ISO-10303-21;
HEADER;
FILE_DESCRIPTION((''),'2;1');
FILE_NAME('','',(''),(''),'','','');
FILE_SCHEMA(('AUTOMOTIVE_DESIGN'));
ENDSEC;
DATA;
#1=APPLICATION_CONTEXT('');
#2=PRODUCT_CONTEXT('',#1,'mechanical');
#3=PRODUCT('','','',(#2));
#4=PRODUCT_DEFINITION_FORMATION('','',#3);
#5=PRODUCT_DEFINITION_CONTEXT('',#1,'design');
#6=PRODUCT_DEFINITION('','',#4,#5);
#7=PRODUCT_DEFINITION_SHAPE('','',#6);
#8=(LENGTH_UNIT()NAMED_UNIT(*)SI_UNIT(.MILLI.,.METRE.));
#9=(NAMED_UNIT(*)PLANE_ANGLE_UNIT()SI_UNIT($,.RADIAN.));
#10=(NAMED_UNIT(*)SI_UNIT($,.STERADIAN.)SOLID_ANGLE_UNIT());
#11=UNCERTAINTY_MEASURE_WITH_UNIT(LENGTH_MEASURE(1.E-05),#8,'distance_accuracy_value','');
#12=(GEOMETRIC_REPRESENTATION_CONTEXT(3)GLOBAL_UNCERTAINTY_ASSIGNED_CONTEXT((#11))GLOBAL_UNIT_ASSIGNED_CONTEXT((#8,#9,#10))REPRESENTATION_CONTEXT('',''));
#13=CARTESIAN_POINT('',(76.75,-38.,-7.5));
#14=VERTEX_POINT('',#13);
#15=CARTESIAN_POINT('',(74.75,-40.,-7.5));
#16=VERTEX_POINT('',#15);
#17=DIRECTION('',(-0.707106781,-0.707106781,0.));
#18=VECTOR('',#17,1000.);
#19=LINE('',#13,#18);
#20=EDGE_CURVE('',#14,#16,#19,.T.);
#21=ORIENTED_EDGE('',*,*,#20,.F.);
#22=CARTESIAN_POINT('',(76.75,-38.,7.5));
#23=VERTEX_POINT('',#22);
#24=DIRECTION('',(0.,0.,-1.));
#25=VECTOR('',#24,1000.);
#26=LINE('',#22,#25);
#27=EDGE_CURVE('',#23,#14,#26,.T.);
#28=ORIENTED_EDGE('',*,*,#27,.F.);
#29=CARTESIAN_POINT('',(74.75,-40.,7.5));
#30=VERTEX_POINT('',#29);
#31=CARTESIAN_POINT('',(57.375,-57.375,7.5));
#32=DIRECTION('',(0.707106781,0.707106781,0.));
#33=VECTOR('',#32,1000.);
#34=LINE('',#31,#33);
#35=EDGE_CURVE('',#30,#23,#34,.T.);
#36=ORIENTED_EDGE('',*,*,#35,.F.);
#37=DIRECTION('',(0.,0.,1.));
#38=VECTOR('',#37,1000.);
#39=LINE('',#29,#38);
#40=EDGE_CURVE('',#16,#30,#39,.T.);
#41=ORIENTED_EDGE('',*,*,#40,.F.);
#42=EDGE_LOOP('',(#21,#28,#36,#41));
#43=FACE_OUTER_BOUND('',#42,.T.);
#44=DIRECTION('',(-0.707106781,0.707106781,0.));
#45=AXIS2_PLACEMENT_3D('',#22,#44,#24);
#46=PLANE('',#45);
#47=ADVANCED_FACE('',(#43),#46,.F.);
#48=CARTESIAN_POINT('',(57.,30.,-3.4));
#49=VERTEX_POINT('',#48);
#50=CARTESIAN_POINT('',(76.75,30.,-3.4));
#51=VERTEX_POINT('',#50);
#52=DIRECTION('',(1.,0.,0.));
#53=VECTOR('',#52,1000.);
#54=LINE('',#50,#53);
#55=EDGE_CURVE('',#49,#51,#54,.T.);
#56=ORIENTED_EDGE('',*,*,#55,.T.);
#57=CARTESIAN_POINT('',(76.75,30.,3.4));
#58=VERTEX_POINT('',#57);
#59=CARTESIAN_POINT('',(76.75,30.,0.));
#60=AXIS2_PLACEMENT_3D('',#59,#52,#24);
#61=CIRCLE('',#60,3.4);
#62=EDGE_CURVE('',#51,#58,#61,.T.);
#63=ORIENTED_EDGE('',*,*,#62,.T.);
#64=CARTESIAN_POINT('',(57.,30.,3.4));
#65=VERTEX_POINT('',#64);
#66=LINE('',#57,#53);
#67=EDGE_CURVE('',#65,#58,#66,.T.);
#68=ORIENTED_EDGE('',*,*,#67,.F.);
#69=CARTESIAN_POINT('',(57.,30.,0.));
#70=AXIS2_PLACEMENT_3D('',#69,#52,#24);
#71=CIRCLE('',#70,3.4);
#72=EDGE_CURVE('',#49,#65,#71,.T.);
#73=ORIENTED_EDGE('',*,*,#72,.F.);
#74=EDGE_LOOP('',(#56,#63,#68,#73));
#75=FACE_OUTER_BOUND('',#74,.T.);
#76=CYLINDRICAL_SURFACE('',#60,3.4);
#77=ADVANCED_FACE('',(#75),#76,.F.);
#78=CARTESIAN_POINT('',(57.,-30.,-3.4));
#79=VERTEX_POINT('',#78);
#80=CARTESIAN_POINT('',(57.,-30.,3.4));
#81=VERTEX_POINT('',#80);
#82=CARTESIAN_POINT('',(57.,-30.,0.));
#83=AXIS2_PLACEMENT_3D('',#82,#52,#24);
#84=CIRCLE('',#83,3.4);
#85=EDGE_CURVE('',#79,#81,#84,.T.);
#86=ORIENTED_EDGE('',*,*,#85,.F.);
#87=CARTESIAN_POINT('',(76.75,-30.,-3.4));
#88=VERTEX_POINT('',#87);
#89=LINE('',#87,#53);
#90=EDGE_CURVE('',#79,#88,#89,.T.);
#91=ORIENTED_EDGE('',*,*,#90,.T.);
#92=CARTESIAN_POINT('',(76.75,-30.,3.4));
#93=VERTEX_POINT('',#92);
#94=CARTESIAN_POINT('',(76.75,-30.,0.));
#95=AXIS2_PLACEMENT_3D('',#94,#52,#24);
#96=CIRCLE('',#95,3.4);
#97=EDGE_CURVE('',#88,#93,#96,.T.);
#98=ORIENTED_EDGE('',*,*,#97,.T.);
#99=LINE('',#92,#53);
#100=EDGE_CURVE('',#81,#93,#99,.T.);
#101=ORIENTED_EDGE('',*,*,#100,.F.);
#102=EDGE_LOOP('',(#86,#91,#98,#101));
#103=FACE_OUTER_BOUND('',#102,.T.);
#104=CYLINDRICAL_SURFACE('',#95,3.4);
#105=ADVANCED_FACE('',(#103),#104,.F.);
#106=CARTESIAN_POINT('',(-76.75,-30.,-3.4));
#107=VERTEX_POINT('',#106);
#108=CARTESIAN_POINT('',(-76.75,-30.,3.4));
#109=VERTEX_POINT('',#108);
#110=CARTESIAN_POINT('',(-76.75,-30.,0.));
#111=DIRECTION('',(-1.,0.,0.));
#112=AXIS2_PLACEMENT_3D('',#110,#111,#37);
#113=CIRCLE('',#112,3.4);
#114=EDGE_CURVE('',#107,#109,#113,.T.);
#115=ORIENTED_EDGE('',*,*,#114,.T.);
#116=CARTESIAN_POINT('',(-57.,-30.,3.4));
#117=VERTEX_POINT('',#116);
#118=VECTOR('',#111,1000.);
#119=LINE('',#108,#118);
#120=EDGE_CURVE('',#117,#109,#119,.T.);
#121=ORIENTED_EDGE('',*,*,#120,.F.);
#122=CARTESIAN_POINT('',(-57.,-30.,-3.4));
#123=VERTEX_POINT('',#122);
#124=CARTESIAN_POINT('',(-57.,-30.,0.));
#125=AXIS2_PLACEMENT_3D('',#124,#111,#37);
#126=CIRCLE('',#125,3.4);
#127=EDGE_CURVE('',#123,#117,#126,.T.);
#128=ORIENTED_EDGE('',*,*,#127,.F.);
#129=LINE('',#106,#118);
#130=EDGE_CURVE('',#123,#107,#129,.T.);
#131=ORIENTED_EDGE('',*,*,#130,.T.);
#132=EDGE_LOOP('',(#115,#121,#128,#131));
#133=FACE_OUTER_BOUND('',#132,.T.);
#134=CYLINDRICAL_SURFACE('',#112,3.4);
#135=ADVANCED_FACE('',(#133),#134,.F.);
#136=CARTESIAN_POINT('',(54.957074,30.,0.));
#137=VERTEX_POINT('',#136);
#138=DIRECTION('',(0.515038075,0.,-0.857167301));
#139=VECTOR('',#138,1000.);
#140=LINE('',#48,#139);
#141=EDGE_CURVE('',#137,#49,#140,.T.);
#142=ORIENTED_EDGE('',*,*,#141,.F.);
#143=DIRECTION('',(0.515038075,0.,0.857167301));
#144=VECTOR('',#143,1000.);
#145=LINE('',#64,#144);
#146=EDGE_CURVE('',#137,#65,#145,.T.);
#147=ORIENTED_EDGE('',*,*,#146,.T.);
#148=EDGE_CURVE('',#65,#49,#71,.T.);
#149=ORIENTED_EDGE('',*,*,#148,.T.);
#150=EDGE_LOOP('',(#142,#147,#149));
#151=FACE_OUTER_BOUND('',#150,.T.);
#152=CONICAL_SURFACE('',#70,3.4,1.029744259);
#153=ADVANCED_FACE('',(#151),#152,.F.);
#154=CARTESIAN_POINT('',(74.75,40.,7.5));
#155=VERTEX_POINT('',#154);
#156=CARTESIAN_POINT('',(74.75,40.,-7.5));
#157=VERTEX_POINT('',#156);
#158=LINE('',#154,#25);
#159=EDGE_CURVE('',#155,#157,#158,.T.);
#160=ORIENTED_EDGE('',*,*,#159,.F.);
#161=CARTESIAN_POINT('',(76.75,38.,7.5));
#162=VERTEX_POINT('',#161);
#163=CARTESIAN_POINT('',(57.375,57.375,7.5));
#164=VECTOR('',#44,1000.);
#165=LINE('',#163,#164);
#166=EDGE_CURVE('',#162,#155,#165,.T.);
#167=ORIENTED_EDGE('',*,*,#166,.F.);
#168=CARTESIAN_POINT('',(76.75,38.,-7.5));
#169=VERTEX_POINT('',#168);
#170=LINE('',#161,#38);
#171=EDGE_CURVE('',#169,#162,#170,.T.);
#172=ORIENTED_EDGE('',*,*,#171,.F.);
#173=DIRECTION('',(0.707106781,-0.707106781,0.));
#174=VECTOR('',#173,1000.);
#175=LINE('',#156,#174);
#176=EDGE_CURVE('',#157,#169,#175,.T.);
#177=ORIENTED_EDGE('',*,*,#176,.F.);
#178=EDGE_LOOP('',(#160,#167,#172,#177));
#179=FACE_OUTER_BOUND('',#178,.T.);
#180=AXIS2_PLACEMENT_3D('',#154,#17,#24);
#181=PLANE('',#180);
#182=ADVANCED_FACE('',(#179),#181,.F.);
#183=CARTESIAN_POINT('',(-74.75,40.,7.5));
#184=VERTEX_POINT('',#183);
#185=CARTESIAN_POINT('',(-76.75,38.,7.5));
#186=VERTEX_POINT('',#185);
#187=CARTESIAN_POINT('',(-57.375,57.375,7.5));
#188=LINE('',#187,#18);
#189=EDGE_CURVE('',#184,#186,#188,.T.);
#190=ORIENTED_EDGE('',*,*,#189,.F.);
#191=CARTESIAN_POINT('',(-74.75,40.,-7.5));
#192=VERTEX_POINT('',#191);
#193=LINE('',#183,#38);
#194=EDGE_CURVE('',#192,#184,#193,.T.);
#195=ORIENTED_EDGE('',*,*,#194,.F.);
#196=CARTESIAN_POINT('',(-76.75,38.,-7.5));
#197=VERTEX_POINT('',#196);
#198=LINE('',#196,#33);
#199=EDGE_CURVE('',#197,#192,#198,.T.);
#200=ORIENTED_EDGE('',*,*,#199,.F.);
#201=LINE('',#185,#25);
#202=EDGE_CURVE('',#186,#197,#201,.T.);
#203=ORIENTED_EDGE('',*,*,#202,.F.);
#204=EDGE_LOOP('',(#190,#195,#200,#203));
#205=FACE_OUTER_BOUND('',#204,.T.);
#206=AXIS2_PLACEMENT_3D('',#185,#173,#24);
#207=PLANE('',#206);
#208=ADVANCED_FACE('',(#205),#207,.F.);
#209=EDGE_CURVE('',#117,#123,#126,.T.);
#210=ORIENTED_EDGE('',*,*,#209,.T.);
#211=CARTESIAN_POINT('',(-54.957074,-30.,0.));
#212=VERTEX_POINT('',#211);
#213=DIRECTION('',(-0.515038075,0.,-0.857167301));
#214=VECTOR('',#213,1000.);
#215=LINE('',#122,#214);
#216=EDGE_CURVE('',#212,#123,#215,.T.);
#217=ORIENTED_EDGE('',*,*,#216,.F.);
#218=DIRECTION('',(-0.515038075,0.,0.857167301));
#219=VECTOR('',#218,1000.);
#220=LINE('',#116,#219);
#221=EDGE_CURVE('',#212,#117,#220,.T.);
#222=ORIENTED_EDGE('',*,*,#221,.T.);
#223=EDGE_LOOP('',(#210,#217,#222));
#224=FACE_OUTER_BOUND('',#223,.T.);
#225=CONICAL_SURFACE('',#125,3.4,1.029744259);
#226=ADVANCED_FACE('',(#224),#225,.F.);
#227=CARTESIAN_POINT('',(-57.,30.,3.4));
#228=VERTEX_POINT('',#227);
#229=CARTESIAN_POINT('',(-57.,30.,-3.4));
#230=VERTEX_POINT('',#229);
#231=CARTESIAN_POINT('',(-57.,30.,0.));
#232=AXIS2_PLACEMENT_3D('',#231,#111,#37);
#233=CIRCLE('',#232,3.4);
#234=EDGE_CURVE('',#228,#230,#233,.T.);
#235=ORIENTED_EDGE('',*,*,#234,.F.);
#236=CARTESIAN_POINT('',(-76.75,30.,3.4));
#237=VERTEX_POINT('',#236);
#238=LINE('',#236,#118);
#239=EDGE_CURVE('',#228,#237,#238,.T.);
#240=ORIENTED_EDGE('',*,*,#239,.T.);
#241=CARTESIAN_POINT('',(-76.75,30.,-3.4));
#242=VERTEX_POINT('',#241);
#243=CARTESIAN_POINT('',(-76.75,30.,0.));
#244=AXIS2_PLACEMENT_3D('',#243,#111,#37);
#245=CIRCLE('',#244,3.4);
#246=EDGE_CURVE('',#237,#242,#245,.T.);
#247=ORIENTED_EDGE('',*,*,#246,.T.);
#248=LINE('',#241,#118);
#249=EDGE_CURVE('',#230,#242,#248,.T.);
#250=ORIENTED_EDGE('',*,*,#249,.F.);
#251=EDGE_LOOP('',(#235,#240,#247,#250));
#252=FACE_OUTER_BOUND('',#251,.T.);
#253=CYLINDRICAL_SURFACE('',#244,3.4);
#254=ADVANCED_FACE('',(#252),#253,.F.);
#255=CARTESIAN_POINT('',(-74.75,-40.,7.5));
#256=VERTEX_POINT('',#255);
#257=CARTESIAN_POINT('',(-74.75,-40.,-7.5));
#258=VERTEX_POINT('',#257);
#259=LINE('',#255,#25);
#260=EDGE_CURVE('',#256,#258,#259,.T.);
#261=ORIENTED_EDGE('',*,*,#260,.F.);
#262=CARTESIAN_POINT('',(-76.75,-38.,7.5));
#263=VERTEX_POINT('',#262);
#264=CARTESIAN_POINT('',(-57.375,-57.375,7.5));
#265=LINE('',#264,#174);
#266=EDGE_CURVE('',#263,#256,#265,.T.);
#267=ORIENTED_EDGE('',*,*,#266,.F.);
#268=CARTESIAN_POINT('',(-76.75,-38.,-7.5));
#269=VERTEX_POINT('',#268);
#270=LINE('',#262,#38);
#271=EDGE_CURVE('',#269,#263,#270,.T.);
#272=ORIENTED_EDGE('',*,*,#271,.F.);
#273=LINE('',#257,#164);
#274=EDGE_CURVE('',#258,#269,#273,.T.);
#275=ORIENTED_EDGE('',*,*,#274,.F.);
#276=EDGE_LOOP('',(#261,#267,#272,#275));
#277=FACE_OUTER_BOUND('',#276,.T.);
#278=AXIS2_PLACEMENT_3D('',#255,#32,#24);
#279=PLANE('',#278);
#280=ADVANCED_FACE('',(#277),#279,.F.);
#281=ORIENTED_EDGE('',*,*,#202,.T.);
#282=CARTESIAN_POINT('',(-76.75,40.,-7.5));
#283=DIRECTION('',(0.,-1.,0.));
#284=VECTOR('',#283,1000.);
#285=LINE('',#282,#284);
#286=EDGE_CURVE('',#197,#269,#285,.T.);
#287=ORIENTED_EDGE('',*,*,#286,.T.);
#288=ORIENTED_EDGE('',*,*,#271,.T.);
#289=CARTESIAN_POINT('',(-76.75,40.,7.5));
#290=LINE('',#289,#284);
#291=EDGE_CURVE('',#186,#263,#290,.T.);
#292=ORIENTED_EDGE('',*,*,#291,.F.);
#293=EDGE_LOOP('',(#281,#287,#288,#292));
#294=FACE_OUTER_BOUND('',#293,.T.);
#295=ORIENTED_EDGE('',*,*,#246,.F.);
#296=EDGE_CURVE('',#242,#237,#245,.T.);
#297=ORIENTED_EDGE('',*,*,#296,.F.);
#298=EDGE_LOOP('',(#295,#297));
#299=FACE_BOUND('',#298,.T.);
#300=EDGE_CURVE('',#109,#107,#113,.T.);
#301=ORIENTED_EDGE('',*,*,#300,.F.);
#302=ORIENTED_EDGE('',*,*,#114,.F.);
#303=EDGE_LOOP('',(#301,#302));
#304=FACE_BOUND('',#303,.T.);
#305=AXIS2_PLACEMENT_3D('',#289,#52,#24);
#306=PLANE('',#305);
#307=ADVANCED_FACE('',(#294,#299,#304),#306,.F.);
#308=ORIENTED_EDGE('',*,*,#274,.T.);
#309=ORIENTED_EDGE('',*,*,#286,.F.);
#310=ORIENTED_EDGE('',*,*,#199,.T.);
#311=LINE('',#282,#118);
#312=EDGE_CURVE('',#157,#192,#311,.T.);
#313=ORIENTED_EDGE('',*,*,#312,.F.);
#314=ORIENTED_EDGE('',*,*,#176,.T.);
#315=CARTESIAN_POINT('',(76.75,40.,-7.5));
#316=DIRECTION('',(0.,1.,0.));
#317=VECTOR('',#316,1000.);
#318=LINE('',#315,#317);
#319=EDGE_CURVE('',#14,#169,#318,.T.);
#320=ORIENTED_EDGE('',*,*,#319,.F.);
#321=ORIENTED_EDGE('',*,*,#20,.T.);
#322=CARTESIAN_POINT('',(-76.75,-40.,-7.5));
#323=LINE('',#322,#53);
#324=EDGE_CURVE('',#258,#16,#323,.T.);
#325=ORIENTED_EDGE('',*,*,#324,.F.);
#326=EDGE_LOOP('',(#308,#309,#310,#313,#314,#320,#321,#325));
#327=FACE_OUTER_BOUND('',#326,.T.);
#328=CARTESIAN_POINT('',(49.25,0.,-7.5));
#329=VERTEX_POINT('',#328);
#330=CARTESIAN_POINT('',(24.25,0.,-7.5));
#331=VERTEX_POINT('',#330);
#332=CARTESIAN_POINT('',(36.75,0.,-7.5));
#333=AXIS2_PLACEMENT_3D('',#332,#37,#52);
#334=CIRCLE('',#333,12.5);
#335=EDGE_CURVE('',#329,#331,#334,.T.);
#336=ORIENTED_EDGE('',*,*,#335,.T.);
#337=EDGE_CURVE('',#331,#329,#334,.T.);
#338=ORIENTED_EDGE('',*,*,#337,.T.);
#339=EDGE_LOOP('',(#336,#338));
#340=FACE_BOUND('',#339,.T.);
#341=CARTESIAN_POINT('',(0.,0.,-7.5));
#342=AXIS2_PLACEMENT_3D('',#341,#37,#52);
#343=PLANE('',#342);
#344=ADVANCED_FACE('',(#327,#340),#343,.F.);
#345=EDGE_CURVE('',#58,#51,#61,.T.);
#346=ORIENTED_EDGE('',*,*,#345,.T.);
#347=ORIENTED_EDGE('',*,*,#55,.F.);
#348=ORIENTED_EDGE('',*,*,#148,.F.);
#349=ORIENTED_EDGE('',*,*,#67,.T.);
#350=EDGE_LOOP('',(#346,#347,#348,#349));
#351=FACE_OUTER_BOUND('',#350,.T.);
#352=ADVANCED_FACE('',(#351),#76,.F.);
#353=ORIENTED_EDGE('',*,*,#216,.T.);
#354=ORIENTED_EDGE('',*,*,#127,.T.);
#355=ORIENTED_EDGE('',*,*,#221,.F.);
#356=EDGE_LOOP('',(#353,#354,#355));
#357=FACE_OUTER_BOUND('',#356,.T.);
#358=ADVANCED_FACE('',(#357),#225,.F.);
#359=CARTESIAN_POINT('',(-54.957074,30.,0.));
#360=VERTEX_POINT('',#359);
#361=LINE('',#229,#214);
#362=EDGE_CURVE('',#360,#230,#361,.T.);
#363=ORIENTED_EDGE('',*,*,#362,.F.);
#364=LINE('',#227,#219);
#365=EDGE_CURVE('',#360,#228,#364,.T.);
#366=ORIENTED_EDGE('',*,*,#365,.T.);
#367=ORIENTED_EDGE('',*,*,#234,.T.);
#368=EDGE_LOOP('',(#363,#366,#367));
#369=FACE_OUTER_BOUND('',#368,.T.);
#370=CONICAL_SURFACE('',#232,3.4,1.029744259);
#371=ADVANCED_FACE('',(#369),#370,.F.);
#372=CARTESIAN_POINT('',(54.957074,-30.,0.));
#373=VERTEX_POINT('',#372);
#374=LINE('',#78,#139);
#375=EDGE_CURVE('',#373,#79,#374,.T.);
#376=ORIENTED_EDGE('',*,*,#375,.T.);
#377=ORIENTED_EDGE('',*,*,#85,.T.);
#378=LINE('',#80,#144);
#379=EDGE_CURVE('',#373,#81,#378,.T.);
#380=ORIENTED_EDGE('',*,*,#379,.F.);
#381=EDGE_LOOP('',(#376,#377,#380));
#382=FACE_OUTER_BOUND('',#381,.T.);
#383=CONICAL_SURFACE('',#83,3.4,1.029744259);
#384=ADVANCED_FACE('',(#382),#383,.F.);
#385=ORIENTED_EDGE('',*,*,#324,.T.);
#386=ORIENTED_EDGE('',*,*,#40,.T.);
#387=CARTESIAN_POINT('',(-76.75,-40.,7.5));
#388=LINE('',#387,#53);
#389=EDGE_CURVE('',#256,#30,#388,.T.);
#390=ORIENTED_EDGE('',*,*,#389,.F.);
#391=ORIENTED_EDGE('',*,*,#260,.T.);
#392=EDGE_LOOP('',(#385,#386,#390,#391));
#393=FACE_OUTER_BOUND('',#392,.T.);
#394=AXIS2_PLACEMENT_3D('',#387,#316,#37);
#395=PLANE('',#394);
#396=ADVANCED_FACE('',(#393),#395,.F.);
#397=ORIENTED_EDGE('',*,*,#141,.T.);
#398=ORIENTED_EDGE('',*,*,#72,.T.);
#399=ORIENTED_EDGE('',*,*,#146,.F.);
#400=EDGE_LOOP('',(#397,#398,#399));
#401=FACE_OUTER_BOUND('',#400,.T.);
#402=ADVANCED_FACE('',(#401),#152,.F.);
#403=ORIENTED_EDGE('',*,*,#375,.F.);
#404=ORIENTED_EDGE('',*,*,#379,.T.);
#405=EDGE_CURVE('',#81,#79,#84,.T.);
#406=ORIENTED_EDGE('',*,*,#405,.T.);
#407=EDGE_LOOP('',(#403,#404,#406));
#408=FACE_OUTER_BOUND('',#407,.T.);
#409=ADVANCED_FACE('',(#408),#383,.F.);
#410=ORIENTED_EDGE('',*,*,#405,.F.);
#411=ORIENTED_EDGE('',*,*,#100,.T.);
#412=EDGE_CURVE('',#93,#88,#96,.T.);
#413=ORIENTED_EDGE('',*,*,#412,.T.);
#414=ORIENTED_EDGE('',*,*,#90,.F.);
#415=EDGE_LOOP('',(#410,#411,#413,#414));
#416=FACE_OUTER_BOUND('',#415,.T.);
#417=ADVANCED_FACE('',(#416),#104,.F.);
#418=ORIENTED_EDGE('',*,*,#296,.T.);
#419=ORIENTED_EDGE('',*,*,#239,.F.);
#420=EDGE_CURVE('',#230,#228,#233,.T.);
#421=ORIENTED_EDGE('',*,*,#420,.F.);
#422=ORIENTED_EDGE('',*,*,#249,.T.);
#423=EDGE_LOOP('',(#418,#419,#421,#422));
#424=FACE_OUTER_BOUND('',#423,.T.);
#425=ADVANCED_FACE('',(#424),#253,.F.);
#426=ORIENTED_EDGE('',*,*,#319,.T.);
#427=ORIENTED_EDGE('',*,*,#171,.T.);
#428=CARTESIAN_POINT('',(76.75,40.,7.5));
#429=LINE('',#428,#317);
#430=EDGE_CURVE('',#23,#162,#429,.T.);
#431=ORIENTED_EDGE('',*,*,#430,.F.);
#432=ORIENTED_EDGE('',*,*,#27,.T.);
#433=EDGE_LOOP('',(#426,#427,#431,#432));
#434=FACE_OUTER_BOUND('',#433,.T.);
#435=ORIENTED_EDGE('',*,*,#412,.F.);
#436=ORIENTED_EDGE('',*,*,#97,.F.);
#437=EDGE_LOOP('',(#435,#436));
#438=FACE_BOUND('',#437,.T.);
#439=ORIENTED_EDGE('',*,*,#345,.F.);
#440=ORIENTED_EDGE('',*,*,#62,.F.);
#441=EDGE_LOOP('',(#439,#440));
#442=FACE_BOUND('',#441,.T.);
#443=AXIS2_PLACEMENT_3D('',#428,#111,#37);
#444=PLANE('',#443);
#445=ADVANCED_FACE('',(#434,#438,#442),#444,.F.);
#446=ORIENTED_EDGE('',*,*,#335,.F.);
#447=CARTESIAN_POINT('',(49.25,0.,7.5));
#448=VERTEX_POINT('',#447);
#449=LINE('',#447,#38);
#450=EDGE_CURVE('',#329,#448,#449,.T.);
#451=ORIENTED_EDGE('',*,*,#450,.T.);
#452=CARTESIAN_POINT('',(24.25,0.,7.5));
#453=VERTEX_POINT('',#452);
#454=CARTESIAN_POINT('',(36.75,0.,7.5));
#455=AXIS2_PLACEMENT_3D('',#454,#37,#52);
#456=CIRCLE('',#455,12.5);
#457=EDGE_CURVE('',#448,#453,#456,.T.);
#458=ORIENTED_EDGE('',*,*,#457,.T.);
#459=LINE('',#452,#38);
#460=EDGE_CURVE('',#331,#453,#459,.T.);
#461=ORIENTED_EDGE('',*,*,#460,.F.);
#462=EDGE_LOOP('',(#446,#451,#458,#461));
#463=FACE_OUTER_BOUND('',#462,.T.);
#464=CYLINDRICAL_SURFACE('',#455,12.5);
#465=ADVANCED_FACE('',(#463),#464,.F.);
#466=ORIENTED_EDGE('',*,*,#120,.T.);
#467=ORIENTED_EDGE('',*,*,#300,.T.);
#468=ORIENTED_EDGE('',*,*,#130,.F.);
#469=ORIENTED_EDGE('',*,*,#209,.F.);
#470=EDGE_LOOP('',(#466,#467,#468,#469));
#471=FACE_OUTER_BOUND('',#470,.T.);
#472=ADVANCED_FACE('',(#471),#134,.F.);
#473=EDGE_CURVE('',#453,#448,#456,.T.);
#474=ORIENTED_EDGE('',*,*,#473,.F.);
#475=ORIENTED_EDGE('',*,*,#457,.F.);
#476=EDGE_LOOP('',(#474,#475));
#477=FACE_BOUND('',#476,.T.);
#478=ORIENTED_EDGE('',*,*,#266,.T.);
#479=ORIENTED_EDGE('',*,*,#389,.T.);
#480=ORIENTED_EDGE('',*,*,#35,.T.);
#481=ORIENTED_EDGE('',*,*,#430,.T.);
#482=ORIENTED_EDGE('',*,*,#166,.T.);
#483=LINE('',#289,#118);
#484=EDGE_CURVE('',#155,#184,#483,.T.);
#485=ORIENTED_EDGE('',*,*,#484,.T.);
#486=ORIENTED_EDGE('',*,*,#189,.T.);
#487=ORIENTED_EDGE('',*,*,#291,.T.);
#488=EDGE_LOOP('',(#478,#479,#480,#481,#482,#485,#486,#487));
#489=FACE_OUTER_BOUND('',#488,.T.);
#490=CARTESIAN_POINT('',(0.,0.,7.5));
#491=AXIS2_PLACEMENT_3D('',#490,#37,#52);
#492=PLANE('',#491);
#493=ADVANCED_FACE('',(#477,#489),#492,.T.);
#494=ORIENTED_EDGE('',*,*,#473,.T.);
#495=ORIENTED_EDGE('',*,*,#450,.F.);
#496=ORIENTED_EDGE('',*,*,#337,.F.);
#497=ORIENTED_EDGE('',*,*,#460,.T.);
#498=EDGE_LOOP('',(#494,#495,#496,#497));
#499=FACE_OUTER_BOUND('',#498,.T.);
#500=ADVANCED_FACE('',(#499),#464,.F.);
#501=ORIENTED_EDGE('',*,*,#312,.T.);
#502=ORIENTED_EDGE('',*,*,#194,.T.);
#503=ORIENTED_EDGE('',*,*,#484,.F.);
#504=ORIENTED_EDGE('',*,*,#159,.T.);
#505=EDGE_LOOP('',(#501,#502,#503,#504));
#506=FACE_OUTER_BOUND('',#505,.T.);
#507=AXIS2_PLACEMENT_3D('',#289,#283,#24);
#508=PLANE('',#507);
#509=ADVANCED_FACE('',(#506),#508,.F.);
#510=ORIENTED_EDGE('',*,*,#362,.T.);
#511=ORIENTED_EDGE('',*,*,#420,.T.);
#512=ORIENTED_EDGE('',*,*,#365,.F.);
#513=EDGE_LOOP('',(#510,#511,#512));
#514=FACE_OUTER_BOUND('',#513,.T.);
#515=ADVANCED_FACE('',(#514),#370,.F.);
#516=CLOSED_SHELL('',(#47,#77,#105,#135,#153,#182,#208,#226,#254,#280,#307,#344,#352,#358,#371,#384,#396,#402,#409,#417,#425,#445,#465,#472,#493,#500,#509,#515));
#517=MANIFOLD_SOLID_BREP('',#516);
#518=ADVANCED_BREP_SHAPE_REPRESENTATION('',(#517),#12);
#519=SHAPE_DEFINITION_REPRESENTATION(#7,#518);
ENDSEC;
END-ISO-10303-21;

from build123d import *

# Parameters (mm, degrees)
SKETCH_1_W                  = 153.5
SKETCH_1_H                  = 80
EXTRUDE_1_DEPTH             = 7.5
HOLE_WIZARD_25_0_25_1_D     = 25
HOLE_WIZARD_M8_1_AT_2_COUNT = 2
HOLE_WIZARD_M8_1_AT_2_PITCH = 60
CHAMFER_1_SIZE              = 2


with BuildPart() as part:
    # 草图1 → 凸台-拉伸1 (new, symmetric)
    with BuildSketch(Plane.XY):
        Rectangle(SKETCH_1_W, SKETCH_1_H)
    extrude(amount=EXTRUDE_1_DEPTH, both=True)

    # Ø25.0 (25) 直径孔1 (through all)
    with Locations(Plane.XY.offset(7.5)):
        with Locations((36.75, 0)):
            Hole(HOLE_WIZARD_25_0_25_1_D / 2)

    # 草图4 → M8 螺纹孔1 (revolve, cut)
    with BuildSketch(Plane(origin=(76.75, 30, 0), x_dir=(0, 0, -1), z_dir=(0, 1, 0))):
        Polygon((0, 0), (0, 21.792926105), (3.4, 19.75), (3.4, 0), align=None)
    hole_wizard_m8_1 = revolve(axis=Axis((83.1, 30, 0), (-1, 0, 0)), mode=Mode.SUBTRACT)

    # M8 螺纹孔1 at 2: M8 螺纹孔1 ×2
    with Locations(*[(0, -i * HOLE_WIZARD_M8_1_AT_2_PITCH, 0) for i in range(1, HOLE_WIZARD_M8_1_AT_2_COUNT)]):
        add(hole_wizard_m8_1, mode=Mode.SUBTRACT)

    # 镜向1: M8 螺纹孔1 across plane
    add(hole_wizard_m8_1.mirror(Plane(origin=(0, 0, 0), x_dir=(0, 0, 1), z_dir=(1, 0, 0))), mode=Mode.SUBTRACT)

    # 镜向1 copy 1 sketch → 镜向1 copy 1 (revolve, cut)
    with BuildSketch(Plane(origin=(-76.75, -30, 0), x_dir=(0, 0, -1), z_dir=(0, 1, 0))):
        Polygon((0, 0), (0, -21.792926105), (3.4, -19.75), (3.4, 0), align=None)
    revolve(axis=Axis((-83.1, -30, 0), (-1, 0, 0)), mode=Mode.SUBTRACT)

    # 倒角1
    chamfer_1_edges = [part.edges().sort_by_distance(p)[0] for p in [
        (76.75, -40, 0),
        (-76.75, -40, 0),
        (-76.75, 40, 0),
        (76.75, 40, 0),
    ]]
    chamfer(chamfer_1_edges, length=CHAMFER_1_SIZE)


solid = part.part
